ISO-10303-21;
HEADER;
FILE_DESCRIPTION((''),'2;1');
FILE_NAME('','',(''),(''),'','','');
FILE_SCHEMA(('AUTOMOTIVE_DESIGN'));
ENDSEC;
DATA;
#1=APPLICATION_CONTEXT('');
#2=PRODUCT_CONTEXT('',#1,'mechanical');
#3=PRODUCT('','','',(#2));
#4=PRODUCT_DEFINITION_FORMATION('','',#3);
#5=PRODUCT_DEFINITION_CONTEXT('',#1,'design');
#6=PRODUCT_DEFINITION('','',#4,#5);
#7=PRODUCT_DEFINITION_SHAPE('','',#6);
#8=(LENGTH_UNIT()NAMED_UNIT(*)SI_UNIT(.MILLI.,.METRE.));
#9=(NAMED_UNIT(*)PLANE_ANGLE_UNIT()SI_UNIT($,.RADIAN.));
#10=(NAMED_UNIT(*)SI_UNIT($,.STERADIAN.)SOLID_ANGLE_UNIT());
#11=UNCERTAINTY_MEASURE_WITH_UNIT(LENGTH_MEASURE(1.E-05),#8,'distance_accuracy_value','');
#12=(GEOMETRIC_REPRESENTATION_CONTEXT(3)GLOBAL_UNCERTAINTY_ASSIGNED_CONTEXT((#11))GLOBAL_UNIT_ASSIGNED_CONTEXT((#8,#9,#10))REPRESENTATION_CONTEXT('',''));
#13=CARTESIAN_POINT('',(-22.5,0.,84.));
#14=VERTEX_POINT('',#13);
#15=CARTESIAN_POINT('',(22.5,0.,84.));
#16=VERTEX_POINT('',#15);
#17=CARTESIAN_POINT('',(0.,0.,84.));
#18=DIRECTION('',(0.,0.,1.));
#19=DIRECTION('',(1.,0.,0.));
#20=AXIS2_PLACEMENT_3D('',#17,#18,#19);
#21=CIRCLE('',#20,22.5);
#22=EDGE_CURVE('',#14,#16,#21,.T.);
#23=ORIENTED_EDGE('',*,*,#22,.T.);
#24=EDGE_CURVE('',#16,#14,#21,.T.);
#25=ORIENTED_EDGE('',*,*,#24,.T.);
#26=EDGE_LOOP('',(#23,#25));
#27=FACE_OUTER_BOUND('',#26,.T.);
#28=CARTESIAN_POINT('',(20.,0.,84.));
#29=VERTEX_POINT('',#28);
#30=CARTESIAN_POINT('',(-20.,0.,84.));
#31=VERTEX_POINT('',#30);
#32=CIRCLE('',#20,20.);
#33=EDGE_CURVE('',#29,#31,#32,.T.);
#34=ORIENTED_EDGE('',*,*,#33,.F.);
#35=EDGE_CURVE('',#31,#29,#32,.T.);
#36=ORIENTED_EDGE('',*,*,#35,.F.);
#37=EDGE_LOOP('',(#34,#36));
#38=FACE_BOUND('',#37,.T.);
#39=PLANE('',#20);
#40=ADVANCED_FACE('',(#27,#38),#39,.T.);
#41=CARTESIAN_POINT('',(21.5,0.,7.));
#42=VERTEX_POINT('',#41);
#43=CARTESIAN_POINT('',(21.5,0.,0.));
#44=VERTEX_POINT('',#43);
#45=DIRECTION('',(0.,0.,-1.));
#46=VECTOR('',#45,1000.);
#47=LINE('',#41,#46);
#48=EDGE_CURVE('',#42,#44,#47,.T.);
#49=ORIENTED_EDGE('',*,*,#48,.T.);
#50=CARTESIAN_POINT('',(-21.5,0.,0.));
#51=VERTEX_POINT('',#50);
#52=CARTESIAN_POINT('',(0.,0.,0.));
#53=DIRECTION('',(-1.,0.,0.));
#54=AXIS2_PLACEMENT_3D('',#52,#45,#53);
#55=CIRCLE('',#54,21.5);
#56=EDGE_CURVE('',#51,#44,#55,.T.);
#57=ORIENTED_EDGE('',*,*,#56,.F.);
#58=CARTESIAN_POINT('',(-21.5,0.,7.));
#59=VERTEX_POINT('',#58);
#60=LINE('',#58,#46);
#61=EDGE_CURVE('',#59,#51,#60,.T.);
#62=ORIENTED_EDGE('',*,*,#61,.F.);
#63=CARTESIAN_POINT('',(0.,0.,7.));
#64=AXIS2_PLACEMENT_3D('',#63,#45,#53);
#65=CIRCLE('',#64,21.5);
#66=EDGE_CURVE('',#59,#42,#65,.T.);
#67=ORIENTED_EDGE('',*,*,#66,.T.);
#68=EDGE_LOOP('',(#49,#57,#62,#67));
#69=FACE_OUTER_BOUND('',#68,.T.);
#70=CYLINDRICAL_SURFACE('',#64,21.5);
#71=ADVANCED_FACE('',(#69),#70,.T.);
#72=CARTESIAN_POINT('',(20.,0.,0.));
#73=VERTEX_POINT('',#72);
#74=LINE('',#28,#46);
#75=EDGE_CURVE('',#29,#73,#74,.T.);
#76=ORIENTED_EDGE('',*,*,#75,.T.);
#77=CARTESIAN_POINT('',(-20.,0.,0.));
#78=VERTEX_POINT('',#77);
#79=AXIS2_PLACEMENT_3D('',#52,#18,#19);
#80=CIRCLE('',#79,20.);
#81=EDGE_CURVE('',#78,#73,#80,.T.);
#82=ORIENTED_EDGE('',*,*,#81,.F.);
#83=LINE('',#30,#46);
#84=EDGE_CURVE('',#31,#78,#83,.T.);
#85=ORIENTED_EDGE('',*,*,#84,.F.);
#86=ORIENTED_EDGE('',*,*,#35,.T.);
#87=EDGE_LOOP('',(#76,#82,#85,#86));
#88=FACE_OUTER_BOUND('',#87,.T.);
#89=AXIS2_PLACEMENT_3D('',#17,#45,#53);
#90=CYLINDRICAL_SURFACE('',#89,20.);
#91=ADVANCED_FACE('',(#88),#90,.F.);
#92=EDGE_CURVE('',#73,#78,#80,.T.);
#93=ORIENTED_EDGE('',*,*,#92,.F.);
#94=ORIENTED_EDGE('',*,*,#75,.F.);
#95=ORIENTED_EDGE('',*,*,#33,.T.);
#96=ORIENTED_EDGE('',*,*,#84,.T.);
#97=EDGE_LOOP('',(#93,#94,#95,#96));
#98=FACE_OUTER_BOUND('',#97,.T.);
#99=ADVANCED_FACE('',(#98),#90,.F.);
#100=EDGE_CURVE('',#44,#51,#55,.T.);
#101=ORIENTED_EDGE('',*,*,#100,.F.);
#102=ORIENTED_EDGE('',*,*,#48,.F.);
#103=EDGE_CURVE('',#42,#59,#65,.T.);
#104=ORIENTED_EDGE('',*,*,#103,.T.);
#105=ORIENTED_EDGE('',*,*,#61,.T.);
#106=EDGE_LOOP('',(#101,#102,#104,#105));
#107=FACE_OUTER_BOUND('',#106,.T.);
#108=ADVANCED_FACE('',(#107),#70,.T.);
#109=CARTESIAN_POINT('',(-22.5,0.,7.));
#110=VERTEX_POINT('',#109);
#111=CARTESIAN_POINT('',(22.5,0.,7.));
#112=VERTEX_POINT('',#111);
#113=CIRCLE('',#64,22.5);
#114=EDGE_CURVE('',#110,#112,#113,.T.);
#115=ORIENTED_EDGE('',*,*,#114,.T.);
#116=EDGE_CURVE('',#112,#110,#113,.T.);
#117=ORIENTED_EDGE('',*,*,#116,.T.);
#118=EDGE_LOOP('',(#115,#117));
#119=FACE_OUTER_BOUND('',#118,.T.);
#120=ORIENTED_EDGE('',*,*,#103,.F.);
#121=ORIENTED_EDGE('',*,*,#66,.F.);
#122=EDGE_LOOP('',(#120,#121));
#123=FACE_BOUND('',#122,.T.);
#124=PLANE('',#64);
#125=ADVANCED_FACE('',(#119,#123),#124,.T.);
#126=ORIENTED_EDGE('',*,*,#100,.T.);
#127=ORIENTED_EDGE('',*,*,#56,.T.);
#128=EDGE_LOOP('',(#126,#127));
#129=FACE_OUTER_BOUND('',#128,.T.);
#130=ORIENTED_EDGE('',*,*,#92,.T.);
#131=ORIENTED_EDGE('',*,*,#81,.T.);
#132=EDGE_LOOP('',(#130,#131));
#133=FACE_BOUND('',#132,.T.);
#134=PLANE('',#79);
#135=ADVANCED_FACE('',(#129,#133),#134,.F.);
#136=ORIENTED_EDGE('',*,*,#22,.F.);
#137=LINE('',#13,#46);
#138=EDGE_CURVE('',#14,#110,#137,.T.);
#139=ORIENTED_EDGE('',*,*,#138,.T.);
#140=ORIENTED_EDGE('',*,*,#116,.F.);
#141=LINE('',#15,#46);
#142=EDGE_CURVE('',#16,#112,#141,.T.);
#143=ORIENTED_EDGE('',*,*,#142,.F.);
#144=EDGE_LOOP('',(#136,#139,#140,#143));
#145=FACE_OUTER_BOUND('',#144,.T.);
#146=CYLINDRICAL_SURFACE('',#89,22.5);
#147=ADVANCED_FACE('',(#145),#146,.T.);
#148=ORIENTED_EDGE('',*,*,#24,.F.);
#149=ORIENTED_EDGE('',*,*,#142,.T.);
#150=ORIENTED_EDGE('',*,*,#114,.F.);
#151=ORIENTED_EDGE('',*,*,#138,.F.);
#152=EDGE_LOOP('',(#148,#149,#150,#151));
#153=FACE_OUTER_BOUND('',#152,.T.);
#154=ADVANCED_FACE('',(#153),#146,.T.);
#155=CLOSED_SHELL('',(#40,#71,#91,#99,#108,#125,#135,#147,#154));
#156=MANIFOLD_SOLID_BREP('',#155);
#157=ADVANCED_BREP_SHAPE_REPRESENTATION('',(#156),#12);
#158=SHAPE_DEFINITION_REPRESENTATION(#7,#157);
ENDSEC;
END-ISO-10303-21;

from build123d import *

# Parameters (mm, degrees)
SKETCH1_R           = 22.5
SKETCH1_R_2         = 20
BOSS_EXTRUDE1_DEPTH = 84
SKETCH2_R           = 22.5
SKETCH2_R_2         = 21.5
CUT_EXTRUDE1_DEPTH  = 7


with BuildPart() as part:
    # Sketch1 → Boss-Extrude1 (new body)
    with BuildSketch(Plane.XY):
        with Locations(Location((0, 0, 0), (0, 0, 180))):
            Circle(SKETCH1_R)
        with Locations(Location((0, 0, 0), (0, 0, 180))):
            Circle(SKETCH1_R_2, mode=Mode.SUBTRACT)
    extrude(amount=BOSS_EXTRUDE1_DEPTH)

    # Sketch2 → Cut-Extrude1 (cut)
    with BuildSketch(Plane(origin=(0, 0, 0), x_dir=(-1, 0, 0), z_dir=(0, 0, -1))):
        Circle(SKETCH2_R)
        Circle(SKETCH2_R_2, mode=Mode.SUBTRACT)
    extrude(amount=-CUT_EXTRUDE1_DEPTH, mode=Mode.SUBTRACT)


solid = part.part
